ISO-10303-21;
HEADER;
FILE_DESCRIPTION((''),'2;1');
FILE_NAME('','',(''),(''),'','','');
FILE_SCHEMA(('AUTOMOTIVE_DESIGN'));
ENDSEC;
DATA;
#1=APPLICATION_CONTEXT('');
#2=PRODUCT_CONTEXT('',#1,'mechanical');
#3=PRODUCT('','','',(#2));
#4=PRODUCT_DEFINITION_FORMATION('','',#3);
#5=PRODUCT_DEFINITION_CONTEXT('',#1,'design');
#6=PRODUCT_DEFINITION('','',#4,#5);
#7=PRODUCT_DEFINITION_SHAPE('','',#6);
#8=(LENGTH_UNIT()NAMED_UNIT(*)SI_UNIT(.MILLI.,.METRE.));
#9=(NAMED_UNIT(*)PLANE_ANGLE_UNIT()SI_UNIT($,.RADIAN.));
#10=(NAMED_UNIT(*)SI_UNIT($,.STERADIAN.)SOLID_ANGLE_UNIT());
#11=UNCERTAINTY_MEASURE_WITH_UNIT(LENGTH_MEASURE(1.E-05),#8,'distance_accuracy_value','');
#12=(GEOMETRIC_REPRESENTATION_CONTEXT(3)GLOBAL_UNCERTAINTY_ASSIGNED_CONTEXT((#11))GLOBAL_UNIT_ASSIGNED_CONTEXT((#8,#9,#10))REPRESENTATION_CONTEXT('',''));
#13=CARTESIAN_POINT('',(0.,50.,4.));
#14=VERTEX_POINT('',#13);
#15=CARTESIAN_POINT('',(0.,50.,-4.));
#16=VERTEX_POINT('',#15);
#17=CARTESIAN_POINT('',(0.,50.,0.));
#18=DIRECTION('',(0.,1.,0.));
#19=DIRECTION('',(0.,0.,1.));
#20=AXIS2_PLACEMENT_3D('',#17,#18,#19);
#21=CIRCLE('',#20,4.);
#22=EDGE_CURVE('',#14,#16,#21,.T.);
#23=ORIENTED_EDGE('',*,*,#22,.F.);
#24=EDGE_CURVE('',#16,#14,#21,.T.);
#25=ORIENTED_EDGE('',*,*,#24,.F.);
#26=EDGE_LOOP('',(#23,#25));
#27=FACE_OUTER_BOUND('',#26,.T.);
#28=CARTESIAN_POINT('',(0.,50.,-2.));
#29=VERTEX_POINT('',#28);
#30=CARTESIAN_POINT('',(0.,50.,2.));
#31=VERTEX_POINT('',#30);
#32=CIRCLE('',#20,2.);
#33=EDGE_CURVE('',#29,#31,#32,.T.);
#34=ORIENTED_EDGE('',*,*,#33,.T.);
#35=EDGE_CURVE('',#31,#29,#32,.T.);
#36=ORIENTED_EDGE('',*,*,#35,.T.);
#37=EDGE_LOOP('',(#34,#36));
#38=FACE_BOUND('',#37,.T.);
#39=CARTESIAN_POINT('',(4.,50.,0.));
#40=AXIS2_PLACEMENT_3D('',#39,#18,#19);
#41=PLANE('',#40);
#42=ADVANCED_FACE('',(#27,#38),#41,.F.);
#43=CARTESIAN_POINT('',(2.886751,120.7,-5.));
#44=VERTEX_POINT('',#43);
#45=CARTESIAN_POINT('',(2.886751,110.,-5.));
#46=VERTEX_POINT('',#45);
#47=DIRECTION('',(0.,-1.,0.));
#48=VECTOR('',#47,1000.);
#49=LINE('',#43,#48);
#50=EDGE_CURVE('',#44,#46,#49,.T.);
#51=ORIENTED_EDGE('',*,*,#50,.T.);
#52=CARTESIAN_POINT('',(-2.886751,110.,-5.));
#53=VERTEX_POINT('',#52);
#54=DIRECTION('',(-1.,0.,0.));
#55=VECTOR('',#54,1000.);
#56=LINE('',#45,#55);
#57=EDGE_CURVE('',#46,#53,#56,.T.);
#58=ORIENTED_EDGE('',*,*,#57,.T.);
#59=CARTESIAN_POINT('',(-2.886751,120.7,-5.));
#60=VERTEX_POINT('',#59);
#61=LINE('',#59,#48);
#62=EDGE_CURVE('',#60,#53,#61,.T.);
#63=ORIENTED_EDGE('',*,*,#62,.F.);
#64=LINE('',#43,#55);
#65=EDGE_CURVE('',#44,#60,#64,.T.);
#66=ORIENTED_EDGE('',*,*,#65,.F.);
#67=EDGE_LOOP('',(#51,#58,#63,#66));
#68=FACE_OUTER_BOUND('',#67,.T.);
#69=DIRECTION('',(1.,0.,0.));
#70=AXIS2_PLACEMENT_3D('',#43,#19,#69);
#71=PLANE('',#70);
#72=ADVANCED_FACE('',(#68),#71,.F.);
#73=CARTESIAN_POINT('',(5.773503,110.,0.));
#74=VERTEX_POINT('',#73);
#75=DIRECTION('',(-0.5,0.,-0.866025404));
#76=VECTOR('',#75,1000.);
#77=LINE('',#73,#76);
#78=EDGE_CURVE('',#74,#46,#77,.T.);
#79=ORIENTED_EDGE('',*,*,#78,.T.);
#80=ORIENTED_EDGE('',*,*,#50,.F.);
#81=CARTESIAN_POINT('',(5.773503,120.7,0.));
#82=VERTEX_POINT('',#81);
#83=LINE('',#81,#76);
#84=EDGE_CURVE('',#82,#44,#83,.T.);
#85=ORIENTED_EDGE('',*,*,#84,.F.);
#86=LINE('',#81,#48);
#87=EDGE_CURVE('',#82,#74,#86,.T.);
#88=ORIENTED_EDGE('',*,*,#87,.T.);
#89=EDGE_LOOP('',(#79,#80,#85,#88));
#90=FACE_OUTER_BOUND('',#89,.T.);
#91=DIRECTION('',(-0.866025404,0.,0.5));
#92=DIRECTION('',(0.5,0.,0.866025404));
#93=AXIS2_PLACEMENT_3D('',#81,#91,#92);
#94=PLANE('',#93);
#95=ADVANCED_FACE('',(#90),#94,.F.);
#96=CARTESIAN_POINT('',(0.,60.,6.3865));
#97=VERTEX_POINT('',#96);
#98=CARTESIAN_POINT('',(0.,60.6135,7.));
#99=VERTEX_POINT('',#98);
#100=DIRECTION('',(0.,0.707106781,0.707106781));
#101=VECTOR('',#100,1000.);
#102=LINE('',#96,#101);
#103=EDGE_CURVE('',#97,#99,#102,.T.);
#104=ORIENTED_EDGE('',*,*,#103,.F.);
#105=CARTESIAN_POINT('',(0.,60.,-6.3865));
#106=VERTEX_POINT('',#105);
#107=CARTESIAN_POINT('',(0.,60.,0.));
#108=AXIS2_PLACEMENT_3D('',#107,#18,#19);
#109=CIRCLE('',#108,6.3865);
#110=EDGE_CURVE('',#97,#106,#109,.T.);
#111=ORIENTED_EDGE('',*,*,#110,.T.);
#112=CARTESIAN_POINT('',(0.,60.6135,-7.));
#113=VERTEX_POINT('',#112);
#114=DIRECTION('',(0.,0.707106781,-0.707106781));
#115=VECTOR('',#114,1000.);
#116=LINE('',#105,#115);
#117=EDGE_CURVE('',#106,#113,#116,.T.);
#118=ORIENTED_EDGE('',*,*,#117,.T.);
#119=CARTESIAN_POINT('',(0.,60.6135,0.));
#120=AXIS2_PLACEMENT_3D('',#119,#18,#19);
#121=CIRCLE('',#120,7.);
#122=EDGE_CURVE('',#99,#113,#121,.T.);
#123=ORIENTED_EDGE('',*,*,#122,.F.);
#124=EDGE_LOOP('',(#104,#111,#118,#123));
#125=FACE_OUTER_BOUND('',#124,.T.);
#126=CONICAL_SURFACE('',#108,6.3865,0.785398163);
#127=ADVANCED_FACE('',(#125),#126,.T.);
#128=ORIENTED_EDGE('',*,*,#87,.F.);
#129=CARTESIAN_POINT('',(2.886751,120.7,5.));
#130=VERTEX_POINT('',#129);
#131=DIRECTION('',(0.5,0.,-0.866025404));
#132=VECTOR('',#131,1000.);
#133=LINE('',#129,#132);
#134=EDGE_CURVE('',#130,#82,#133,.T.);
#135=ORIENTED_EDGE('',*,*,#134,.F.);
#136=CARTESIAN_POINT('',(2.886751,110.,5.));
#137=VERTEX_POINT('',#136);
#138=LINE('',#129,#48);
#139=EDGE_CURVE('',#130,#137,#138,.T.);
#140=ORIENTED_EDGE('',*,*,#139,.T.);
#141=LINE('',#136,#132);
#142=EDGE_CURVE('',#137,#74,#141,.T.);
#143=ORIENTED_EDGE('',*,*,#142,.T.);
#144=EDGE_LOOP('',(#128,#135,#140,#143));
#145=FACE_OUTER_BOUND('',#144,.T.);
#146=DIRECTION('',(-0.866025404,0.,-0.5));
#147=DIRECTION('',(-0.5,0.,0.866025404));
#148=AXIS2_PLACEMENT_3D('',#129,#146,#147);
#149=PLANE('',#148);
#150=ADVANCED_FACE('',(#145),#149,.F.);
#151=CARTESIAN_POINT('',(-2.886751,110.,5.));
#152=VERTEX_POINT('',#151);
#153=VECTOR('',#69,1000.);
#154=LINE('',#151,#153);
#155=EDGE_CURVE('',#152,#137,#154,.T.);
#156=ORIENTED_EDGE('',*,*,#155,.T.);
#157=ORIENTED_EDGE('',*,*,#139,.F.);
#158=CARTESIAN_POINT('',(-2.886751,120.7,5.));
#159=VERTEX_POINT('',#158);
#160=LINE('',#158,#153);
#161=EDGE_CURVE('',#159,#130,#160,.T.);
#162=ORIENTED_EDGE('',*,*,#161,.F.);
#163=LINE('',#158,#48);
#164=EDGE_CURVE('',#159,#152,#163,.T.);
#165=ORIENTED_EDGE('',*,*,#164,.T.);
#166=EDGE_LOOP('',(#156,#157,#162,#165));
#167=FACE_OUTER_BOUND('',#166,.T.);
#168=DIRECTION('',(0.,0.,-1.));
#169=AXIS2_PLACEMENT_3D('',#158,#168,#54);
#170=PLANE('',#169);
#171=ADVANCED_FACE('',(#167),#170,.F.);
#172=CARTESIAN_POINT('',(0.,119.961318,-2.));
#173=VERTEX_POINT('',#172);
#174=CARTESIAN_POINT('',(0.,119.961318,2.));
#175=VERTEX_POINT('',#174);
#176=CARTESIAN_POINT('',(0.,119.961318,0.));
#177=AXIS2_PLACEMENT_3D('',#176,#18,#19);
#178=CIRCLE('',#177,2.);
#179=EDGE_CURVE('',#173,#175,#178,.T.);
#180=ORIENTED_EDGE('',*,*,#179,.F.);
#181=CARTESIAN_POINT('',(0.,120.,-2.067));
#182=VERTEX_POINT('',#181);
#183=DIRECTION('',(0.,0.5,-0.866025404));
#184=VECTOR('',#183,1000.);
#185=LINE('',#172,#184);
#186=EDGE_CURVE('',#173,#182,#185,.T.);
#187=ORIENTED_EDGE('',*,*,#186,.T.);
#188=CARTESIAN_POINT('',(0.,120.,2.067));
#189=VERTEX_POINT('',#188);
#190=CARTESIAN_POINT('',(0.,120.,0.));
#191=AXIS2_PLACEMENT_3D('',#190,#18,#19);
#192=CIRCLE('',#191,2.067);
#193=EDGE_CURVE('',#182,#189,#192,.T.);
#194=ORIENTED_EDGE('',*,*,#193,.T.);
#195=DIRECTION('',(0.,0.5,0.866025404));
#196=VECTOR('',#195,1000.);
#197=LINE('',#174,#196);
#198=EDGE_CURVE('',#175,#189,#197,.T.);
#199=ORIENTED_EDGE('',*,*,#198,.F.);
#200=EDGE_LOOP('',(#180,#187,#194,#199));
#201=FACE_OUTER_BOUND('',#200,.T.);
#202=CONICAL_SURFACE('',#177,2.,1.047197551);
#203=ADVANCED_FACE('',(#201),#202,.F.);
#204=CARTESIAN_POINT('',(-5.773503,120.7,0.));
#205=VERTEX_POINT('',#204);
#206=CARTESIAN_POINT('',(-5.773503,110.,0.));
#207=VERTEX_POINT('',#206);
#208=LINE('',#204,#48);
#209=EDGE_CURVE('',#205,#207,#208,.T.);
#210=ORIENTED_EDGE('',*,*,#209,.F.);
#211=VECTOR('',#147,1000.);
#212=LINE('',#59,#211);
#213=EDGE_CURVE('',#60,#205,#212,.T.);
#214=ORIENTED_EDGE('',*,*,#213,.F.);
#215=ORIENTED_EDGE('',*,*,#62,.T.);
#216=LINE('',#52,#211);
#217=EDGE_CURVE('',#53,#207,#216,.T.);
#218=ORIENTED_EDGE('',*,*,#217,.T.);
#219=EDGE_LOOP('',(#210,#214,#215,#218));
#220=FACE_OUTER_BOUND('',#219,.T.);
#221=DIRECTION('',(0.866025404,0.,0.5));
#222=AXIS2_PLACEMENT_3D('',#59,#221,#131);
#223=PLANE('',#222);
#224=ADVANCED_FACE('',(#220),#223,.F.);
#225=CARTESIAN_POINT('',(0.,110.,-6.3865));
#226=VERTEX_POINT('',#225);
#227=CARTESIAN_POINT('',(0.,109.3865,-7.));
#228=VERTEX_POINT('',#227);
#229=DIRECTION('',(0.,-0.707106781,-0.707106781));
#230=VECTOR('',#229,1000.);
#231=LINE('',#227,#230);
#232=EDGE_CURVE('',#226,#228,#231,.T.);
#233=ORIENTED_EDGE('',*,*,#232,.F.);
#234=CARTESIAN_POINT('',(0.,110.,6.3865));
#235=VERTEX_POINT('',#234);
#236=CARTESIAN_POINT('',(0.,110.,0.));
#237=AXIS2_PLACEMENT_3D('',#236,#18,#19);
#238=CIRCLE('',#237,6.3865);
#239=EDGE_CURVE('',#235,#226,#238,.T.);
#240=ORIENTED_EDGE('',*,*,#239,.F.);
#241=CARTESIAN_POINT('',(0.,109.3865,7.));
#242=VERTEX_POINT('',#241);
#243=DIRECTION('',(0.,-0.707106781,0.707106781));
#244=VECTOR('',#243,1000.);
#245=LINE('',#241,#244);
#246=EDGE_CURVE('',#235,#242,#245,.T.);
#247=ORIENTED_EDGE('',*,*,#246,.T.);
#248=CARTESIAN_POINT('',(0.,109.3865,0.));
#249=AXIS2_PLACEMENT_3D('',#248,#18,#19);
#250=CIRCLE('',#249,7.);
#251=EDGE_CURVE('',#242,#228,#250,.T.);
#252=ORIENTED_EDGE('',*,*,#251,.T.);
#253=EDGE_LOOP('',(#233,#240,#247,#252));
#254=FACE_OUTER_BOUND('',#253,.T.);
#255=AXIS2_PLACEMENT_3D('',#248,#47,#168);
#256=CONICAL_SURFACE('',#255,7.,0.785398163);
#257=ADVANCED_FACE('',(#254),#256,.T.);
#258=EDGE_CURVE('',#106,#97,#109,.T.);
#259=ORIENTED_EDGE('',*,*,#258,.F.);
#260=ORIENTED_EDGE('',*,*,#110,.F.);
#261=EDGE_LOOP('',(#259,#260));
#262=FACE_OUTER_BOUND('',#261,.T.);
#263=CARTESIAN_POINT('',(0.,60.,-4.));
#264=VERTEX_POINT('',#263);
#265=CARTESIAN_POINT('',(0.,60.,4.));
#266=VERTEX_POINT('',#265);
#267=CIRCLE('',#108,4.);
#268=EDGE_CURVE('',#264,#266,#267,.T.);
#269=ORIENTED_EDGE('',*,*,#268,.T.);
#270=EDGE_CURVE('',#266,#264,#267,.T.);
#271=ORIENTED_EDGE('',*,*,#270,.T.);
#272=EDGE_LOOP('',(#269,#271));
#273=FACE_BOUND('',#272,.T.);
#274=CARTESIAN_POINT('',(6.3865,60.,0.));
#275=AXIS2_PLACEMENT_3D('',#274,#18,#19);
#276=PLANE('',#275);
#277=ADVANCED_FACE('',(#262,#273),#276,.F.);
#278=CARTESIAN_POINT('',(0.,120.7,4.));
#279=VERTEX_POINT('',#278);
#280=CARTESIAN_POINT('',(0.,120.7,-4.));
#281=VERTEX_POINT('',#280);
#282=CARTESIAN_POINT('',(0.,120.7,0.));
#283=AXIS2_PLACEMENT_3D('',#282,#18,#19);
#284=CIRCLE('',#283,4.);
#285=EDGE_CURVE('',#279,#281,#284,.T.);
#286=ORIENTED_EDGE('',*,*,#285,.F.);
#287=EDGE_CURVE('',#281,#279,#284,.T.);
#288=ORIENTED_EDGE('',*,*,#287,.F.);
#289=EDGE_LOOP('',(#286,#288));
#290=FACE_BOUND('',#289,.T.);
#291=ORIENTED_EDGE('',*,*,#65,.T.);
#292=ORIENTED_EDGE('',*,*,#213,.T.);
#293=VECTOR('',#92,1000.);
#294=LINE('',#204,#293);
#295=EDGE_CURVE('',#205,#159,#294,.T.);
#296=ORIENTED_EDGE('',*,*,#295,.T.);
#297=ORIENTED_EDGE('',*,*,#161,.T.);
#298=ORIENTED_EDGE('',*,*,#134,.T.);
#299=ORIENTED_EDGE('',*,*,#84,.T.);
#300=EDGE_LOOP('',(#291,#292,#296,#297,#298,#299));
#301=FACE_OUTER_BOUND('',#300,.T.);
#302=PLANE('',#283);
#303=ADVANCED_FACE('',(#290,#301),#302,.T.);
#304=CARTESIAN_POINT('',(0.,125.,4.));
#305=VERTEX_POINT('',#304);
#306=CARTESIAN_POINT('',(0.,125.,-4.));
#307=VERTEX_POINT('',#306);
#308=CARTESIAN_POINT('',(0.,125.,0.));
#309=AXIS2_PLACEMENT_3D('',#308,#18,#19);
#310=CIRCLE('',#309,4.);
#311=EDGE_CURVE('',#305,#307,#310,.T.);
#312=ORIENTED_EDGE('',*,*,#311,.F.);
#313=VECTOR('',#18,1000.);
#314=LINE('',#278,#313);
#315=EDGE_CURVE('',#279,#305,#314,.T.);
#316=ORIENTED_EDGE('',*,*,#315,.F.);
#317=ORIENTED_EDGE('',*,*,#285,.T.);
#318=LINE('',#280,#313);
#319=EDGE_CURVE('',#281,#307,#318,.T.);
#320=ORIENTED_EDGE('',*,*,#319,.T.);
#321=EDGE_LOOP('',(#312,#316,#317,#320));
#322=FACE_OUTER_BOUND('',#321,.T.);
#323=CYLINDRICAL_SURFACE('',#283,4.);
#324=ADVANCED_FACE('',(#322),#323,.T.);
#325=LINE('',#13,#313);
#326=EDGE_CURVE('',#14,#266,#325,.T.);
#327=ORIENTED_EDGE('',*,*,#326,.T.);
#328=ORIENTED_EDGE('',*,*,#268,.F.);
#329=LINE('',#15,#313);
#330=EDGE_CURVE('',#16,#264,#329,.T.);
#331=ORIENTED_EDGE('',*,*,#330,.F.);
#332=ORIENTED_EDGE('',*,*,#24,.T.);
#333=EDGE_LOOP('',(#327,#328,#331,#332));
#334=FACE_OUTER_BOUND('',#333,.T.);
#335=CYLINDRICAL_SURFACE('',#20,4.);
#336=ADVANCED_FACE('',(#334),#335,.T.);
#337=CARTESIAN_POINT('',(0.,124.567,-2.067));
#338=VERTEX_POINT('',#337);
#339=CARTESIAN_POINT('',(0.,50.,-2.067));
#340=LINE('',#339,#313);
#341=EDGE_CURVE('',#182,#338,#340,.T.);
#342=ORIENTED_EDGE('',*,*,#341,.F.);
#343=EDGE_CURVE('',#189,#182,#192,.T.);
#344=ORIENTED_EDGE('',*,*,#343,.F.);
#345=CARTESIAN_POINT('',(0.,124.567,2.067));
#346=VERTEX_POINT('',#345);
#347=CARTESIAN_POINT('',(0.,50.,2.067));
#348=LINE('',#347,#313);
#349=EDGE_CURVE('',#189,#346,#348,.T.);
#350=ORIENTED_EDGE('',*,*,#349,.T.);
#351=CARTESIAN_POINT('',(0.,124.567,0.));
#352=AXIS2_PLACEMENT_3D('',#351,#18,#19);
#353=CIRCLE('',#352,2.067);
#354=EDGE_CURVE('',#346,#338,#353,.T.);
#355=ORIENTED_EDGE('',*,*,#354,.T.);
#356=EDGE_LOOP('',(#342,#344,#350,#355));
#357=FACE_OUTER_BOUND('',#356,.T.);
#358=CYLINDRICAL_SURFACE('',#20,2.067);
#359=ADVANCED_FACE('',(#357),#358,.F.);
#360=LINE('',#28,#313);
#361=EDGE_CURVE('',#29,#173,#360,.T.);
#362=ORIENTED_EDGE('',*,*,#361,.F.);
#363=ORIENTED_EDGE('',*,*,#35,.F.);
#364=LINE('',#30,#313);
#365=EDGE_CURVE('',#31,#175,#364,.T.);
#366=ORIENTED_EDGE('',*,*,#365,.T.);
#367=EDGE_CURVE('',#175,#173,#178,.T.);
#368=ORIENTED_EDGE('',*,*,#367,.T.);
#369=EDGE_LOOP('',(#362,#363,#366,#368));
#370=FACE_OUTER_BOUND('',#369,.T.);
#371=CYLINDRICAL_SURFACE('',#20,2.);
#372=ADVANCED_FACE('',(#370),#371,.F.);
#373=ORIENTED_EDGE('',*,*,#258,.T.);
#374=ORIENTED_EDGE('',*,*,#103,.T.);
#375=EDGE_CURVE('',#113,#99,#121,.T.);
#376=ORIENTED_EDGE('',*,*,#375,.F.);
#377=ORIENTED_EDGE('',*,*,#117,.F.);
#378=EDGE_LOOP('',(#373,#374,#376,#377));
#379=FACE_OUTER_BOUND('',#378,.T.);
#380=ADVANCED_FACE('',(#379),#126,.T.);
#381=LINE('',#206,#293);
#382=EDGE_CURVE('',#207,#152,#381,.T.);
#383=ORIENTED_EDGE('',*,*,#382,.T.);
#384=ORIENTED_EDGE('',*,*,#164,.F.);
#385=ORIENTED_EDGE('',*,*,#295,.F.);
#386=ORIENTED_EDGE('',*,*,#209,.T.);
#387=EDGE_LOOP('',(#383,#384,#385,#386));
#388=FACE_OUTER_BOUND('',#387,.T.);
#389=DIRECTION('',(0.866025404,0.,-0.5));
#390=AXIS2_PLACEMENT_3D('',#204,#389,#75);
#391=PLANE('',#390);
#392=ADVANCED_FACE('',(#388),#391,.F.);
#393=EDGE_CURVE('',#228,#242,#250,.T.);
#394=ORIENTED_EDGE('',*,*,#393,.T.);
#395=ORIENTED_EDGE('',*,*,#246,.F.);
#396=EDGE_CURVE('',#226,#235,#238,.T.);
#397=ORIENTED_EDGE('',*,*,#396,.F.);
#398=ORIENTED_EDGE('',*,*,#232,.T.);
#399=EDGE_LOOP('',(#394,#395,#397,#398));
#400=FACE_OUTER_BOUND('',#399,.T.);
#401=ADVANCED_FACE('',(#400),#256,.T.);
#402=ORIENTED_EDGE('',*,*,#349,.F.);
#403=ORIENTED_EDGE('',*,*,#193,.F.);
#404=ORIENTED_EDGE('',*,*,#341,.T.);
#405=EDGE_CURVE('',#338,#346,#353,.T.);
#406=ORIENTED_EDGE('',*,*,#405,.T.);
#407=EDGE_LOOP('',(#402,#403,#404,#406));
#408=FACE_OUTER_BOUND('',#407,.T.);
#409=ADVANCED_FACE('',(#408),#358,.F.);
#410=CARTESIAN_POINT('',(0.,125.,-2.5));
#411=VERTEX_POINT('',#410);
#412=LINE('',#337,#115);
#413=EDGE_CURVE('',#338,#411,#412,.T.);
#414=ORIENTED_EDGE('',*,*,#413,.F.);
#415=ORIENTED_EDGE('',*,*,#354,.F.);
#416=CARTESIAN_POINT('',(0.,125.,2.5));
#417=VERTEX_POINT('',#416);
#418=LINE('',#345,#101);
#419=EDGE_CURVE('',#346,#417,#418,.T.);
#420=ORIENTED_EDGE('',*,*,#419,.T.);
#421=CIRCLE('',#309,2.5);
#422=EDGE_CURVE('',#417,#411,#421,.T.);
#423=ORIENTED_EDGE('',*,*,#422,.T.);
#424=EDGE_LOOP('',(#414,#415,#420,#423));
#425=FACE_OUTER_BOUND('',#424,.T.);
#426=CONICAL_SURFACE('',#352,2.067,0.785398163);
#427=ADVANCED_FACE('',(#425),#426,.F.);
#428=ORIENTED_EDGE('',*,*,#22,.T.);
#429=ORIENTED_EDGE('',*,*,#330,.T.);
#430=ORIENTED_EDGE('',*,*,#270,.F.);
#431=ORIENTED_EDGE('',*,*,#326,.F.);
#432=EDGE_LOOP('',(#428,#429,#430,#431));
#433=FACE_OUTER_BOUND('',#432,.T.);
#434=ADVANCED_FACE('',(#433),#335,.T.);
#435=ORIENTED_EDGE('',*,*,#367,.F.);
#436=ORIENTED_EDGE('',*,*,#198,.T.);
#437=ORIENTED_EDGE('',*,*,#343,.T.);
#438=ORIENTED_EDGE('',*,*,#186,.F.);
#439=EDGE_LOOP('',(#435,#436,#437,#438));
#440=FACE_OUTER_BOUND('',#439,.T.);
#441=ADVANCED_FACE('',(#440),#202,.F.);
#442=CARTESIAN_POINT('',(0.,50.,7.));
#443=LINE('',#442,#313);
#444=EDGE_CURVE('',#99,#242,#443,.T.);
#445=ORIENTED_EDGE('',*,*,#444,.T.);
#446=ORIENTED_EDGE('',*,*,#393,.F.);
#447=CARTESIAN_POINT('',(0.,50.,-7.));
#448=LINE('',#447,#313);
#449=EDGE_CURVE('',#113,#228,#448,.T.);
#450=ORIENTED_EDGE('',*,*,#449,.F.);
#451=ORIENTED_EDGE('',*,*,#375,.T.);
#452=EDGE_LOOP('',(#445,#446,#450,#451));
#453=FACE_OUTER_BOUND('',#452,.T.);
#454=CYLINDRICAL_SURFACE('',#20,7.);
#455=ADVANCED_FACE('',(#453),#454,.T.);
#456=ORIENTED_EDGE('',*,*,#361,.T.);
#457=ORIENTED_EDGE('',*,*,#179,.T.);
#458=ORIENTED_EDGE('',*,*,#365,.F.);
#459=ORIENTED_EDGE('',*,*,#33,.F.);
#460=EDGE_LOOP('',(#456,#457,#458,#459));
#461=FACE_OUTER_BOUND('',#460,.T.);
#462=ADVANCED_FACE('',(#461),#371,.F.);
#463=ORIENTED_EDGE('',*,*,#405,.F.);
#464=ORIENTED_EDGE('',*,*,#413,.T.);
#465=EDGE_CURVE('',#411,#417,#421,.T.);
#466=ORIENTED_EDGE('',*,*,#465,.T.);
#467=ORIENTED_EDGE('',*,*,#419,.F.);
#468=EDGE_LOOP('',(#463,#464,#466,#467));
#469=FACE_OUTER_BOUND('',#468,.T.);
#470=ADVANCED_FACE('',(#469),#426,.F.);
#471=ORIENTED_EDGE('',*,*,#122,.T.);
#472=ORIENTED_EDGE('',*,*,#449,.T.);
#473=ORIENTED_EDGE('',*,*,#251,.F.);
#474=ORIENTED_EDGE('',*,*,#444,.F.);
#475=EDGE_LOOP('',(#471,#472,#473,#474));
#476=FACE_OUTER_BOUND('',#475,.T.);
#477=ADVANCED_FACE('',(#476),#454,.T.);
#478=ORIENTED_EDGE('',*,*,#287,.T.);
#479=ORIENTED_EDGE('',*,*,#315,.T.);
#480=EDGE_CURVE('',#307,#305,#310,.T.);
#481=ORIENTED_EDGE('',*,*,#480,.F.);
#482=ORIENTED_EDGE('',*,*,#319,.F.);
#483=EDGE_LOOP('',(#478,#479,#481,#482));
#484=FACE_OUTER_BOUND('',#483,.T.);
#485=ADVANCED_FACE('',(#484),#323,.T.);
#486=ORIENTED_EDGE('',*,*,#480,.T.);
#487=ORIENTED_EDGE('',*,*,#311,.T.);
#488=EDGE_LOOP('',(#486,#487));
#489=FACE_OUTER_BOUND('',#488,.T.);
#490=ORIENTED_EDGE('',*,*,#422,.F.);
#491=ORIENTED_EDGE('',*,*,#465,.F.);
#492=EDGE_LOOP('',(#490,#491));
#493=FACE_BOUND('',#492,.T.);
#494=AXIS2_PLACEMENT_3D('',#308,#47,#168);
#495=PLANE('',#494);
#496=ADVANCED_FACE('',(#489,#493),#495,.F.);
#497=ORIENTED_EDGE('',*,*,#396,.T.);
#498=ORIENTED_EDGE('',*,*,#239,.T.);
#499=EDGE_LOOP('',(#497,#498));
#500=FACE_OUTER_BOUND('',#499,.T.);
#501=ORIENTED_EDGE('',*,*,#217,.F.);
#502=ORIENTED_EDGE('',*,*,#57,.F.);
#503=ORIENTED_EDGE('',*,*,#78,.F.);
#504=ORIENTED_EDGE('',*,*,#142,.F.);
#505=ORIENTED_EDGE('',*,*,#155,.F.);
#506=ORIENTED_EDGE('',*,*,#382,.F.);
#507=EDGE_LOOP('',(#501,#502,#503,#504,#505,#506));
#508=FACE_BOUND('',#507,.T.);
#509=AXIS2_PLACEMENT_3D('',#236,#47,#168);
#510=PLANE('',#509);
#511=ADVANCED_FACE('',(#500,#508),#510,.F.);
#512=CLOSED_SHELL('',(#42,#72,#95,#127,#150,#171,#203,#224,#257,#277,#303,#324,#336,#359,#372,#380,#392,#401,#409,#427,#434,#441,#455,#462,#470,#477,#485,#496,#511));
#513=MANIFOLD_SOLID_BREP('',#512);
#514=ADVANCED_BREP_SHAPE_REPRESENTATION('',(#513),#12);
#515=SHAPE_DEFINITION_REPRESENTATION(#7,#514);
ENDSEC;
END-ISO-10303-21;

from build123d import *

# Parameters (mm, degrees)
BOSS_EXTRUDE1_DEPTH = 10.7
SKETCH3_W           = 4
SKETCH3_H           = 4.3


with BuildPart() as part:
    # Sketch1 → Revolve1 (revolve)
    with BuildSketch(Plane.XY, mode=Mode.PRIVATE) as revolve1_sk:
        Polygon((0, 110), (6.3865, 110), (7, 109.3865), (7, 60.6135), (6.3865, 60), (4, 60), (4, 50), (0, 50), align=None)
    revolve(revolve1_sk.sketch.rotate(Axis((0, 50, 0), (0, 1, 0)), 270), axis=Axis((0, 50, 0), (0, 1, 0)))

    # Sketch2 → Boss-Extrude1 (add)
    with BuildSketch(Plane(origin=(0, 110, 0), x_dir=(1, 0, 0), z_dir=(0, 1, 0))):
        Polygon((-5.773502692, 0), (-2.886751346, -5), (2.886751346, -5), (5.773502692, 0), (2.886751346, 5), (-2.886751346, 5), align=None)
    extrude(amount=BOSS_EXTRUDE1_DEPTH)

    # Sketch3 → Revolve2 (revolve)
    with BuildSketch(Plane.XY, mode=Mode.PRIVATE) as revolve2_sk:
        with Locations((2, 122.85)):
            Rectangle(SKETCH3_W, SKETCH3_H)
    revolve(revolve2_sk.sketch.rotate(Axis((0, 120.7, 0), (0, 1, 0)), 270), axis=Axis((0, 120.7, 0), (0, 1, 0)))

    # Sketch4 → Cut-Revolve1 (revolve, cut)
    with BuildSketch(Plane.XY, mode=Mode.PRIVATE) as cut_revolve1_sk:
        Polygon((0, 125), (2.5, 125), (2.067, 124.567), (2.067, 120), (2, 119.961317532), (2, 50), (0, 50), align=None)
    revolve(cut_revolve1_sk.sketch.rotate(Axis((0, 50, 0), (0, 1, 0)), 270), axis=Axis((0, 50, 0), (0, 1, 0)), mode=Mode.SUBTRACT)


solid = part.part
